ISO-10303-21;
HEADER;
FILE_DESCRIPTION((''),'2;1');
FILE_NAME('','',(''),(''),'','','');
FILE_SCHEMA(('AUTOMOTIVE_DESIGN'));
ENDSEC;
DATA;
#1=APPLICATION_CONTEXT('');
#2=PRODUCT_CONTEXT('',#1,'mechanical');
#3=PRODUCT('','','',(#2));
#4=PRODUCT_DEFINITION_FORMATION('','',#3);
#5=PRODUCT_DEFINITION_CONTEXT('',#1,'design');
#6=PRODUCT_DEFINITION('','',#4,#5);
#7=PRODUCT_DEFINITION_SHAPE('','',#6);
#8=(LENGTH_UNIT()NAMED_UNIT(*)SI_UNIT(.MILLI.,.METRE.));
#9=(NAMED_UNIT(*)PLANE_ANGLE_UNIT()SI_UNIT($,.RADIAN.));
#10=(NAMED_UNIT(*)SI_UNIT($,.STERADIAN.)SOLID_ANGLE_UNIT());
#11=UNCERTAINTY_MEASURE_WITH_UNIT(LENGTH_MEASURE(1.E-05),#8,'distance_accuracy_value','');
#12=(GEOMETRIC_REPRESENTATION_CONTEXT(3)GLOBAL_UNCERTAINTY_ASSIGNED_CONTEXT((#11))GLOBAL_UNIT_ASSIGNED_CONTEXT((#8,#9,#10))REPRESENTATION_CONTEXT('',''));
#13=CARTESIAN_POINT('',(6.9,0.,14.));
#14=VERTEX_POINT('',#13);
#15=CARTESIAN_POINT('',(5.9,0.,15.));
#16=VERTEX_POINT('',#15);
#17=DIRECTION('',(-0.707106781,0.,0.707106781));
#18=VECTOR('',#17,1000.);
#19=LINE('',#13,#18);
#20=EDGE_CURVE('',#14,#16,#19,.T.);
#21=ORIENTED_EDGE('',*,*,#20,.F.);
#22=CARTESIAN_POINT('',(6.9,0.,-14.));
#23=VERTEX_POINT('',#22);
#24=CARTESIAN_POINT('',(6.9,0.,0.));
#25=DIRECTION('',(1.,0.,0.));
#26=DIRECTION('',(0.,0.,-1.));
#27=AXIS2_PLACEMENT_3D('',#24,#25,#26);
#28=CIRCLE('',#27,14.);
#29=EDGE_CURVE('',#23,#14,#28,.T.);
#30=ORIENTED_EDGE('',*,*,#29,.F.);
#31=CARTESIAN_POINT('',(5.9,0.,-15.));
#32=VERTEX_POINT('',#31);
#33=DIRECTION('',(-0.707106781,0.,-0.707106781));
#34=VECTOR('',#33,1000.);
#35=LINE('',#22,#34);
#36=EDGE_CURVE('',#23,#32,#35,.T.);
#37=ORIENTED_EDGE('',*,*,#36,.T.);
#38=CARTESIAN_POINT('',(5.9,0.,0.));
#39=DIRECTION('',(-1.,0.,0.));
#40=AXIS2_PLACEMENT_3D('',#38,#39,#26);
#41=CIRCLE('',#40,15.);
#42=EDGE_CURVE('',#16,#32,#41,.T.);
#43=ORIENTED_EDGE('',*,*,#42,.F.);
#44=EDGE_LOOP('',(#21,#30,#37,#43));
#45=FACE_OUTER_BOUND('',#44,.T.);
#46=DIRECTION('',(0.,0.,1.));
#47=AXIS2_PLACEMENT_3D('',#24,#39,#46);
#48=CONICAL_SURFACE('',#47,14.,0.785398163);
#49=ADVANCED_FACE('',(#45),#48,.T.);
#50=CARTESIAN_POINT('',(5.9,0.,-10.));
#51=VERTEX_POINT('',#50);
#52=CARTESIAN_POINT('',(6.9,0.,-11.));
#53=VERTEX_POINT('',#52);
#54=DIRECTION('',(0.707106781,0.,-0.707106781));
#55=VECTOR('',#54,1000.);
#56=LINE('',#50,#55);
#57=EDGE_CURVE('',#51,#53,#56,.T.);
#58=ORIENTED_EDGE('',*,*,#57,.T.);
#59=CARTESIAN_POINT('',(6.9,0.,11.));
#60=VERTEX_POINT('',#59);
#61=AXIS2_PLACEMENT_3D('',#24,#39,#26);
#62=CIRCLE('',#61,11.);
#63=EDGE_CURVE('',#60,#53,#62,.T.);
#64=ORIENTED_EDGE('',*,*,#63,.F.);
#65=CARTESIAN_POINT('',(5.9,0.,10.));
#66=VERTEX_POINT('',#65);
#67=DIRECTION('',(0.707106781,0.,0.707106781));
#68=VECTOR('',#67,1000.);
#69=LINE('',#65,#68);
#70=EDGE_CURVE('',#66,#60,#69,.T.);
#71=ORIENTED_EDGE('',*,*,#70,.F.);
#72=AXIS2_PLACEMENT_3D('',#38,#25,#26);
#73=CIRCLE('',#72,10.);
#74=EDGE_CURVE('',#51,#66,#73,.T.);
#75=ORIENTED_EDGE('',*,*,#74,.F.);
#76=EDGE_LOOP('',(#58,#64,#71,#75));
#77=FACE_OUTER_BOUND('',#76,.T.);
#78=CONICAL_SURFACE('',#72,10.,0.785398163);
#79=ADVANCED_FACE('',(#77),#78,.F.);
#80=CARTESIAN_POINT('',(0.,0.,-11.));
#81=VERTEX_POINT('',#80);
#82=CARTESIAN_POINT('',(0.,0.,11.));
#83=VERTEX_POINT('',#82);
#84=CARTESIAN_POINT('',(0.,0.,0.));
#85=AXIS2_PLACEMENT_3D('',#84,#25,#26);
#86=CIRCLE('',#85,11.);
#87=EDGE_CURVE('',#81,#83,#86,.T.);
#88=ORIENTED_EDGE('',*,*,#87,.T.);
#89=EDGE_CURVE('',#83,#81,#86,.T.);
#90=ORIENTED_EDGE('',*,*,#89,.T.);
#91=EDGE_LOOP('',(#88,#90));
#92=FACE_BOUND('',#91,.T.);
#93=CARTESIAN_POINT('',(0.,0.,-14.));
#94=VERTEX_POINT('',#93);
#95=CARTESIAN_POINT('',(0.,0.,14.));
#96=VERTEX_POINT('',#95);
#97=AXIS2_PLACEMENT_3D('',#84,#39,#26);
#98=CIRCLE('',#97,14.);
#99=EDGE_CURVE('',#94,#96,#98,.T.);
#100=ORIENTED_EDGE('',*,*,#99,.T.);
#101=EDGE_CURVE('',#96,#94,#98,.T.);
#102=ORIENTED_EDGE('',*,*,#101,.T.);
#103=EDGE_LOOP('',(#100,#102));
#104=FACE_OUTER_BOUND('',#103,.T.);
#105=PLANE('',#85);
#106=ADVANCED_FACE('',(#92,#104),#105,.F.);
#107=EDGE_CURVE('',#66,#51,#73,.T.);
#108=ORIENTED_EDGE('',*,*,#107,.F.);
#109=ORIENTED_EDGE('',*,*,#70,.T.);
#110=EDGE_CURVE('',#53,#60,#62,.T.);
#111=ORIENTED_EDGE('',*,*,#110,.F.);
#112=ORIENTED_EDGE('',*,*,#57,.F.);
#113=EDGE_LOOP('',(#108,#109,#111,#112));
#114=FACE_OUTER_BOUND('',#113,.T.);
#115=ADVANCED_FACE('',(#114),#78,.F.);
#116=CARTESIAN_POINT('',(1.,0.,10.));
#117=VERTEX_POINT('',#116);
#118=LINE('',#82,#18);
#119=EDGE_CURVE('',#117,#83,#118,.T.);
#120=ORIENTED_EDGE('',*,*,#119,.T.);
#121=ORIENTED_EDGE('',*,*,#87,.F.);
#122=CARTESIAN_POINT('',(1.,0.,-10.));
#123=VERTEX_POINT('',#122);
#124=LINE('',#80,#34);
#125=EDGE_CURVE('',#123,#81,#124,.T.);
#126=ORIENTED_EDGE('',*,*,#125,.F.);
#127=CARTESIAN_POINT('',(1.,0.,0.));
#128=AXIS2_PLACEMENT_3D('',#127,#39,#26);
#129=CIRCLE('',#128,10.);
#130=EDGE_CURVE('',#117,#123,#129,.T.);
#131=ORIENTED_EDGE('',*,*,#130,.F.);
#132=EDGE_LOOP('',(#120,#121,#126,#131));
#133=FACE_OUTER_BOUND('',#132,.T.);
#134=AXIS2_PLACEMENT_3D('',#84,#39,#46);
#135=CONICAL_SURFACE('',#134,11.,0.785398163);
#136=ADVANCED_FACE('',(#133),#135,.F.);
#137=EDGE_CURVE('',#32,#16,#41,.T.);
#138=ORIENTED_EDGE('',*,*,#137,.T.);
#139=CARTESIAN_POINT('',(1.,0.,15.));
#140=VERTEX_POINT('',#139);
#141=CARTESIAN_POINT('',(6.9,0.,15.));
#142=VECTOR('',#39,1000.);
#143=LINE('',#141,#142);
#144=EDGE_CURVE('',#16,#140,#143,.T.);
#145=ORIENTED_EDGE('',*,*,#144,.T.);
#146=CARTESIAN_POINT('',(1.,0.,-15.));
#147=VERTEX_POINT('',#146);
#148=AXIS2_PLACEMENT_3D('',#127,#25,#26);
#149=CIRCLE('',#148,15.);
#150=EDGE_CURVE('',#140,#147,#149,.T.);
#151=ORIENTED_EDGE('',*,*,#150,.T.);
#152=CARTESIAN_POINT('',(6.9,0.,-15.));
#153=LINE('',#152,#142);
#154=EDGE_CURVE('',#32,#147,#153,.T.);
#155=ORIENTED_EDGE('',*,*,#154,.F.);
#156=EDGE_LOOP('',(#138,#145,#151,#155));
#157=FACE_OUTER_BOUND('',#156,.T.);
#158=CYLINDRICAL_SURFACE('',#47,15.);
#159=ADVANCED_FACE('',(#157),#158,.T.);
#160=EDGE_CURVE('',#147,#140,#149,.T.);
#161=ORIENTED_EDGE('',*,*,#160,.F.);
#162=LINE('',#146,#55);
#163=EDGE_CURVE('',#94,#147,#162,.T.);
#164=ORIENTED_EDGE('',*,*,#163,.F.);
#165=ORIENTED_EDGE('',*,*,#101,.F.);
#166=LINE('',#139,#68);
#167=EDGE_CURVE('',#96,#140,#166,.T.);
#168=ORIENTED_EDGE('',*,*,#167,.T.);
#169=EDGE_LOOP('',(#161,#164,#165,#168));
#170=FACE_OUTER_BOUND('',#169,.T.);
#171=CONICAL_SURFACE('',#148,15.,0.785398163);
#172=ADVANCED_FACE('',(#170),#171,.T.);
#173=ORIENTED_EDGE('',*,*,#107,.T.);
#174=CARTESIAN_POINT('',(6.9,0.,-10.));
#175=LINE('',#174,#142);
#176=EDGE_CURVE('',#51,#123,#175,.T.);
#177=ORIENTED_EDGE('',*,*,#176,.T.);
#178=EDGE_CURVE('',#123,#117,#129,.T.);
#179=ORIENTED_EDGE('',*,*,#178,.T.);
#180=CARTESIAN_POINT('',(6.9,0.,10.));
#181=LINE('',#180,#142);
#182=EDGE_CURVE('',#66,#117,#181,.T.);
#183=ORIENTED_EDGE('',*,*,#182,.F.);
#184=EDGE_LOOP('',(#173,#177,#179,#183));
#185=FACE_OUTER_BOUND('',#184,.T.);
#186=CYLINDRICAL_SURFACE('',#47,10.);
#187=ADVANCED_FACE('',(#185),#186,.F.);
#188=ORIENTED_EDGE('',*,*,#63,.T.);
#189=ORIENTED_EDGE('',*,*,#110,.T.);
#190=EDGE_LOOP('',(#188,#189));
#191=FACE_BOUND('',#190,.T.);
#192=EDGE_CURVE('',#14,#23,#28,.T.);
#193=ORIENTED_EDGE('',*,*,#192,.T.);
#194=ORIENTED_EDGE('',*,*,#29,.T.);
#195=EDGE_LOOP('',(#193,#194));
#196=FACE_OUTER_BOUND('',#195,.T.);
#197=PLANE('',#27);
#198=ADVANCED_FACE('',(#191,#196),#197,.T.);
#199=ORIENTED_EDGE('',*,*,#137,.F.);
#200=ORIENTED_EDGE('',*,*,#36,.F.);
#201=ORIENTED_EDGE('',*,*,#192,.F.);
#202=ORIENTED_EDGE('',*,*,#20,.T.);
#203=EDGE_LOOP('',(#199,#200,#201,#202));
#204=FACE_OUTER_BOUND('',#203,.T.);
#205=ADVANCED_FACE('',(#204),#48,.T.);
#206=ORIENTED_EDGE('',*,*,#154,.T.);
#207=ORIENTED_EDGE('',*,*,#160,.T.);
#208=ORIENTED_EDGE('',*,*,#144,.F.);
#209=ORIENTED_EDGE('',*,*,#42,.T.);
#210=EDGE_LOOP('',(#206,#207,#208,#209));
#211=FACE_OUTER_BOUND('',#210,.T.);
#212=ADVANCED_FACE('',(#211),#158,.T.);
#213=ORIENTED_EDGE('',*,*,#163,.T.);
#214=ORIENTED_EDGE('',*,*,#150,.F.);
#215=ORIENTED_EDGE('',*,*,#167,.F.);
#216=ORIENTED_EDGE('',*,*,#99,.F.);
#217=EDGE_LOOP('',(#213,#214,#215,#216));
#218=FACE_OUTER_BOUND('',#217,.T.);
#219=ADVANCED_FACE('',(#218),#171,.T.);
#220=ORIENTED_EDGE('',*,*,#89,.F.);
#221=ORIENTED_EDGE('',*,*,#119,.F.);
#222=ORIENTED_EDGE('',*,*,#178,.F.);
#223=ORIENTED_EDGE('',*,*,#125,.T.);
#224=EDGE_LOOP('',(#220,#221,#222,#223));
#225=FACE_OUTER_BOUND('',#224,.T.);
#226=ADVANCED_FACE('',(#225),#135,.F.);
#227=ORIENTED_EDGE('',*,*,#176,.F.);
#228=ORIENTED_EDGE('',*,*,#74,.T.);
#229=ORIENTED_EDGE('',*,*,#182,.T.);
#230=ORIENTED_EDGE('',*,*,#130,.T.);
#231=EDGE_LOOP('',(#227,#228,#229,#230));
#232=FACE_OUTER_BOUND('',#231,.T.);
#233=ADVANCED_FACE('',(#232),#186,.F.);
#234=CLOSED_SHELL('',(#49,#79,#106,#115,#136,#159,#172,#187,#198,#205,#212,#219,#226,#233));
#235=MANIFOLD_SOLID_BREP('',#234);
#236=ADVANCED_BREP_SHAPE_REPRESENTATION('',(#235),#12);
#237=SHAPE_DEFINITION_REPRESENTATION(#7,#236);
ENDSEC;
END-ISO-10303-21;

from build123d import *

# Parameters (mm, degrees)
SKETCH1_R           = 15
SKETCH1_R_2         = 10
BOSS_EXTRUDE1_DEPTH = 6.9
CHAMFER1_SIZE       = 1


with BuildPart() as part:
    # Sketch1 → Boss-Extrude1 (new body)
    with BuildSketch(Plane(origin=(0, 0, 0), x_dir=(0, 0, -1), z_dir=(1, 0, 0))):
        with Locations(Location((0, 0, 0), (0, 0, 180))):
            Circle(SKETCH1_R)
        with Locations(Location((0, 0, 0), (0, 0, 180))):
            Circle(SKETCH1_R_2, mode=Mode.SUBTRACT)
    extrude(amount=BOSS_EXTRUDE1_DEPTH)

    # Chamfer1
    chamfer1_edges = [part.edges().sort_by_distance(p)[0] for p in [
        (0, 0, -15),
        (6.9, 0, -15),
        (0, 0, -10),
        (6.9, 0, -10),
    ]]
    chamfer(chamfer1_edges, length=CHAMFER1_SIZE)


solid = part.part
